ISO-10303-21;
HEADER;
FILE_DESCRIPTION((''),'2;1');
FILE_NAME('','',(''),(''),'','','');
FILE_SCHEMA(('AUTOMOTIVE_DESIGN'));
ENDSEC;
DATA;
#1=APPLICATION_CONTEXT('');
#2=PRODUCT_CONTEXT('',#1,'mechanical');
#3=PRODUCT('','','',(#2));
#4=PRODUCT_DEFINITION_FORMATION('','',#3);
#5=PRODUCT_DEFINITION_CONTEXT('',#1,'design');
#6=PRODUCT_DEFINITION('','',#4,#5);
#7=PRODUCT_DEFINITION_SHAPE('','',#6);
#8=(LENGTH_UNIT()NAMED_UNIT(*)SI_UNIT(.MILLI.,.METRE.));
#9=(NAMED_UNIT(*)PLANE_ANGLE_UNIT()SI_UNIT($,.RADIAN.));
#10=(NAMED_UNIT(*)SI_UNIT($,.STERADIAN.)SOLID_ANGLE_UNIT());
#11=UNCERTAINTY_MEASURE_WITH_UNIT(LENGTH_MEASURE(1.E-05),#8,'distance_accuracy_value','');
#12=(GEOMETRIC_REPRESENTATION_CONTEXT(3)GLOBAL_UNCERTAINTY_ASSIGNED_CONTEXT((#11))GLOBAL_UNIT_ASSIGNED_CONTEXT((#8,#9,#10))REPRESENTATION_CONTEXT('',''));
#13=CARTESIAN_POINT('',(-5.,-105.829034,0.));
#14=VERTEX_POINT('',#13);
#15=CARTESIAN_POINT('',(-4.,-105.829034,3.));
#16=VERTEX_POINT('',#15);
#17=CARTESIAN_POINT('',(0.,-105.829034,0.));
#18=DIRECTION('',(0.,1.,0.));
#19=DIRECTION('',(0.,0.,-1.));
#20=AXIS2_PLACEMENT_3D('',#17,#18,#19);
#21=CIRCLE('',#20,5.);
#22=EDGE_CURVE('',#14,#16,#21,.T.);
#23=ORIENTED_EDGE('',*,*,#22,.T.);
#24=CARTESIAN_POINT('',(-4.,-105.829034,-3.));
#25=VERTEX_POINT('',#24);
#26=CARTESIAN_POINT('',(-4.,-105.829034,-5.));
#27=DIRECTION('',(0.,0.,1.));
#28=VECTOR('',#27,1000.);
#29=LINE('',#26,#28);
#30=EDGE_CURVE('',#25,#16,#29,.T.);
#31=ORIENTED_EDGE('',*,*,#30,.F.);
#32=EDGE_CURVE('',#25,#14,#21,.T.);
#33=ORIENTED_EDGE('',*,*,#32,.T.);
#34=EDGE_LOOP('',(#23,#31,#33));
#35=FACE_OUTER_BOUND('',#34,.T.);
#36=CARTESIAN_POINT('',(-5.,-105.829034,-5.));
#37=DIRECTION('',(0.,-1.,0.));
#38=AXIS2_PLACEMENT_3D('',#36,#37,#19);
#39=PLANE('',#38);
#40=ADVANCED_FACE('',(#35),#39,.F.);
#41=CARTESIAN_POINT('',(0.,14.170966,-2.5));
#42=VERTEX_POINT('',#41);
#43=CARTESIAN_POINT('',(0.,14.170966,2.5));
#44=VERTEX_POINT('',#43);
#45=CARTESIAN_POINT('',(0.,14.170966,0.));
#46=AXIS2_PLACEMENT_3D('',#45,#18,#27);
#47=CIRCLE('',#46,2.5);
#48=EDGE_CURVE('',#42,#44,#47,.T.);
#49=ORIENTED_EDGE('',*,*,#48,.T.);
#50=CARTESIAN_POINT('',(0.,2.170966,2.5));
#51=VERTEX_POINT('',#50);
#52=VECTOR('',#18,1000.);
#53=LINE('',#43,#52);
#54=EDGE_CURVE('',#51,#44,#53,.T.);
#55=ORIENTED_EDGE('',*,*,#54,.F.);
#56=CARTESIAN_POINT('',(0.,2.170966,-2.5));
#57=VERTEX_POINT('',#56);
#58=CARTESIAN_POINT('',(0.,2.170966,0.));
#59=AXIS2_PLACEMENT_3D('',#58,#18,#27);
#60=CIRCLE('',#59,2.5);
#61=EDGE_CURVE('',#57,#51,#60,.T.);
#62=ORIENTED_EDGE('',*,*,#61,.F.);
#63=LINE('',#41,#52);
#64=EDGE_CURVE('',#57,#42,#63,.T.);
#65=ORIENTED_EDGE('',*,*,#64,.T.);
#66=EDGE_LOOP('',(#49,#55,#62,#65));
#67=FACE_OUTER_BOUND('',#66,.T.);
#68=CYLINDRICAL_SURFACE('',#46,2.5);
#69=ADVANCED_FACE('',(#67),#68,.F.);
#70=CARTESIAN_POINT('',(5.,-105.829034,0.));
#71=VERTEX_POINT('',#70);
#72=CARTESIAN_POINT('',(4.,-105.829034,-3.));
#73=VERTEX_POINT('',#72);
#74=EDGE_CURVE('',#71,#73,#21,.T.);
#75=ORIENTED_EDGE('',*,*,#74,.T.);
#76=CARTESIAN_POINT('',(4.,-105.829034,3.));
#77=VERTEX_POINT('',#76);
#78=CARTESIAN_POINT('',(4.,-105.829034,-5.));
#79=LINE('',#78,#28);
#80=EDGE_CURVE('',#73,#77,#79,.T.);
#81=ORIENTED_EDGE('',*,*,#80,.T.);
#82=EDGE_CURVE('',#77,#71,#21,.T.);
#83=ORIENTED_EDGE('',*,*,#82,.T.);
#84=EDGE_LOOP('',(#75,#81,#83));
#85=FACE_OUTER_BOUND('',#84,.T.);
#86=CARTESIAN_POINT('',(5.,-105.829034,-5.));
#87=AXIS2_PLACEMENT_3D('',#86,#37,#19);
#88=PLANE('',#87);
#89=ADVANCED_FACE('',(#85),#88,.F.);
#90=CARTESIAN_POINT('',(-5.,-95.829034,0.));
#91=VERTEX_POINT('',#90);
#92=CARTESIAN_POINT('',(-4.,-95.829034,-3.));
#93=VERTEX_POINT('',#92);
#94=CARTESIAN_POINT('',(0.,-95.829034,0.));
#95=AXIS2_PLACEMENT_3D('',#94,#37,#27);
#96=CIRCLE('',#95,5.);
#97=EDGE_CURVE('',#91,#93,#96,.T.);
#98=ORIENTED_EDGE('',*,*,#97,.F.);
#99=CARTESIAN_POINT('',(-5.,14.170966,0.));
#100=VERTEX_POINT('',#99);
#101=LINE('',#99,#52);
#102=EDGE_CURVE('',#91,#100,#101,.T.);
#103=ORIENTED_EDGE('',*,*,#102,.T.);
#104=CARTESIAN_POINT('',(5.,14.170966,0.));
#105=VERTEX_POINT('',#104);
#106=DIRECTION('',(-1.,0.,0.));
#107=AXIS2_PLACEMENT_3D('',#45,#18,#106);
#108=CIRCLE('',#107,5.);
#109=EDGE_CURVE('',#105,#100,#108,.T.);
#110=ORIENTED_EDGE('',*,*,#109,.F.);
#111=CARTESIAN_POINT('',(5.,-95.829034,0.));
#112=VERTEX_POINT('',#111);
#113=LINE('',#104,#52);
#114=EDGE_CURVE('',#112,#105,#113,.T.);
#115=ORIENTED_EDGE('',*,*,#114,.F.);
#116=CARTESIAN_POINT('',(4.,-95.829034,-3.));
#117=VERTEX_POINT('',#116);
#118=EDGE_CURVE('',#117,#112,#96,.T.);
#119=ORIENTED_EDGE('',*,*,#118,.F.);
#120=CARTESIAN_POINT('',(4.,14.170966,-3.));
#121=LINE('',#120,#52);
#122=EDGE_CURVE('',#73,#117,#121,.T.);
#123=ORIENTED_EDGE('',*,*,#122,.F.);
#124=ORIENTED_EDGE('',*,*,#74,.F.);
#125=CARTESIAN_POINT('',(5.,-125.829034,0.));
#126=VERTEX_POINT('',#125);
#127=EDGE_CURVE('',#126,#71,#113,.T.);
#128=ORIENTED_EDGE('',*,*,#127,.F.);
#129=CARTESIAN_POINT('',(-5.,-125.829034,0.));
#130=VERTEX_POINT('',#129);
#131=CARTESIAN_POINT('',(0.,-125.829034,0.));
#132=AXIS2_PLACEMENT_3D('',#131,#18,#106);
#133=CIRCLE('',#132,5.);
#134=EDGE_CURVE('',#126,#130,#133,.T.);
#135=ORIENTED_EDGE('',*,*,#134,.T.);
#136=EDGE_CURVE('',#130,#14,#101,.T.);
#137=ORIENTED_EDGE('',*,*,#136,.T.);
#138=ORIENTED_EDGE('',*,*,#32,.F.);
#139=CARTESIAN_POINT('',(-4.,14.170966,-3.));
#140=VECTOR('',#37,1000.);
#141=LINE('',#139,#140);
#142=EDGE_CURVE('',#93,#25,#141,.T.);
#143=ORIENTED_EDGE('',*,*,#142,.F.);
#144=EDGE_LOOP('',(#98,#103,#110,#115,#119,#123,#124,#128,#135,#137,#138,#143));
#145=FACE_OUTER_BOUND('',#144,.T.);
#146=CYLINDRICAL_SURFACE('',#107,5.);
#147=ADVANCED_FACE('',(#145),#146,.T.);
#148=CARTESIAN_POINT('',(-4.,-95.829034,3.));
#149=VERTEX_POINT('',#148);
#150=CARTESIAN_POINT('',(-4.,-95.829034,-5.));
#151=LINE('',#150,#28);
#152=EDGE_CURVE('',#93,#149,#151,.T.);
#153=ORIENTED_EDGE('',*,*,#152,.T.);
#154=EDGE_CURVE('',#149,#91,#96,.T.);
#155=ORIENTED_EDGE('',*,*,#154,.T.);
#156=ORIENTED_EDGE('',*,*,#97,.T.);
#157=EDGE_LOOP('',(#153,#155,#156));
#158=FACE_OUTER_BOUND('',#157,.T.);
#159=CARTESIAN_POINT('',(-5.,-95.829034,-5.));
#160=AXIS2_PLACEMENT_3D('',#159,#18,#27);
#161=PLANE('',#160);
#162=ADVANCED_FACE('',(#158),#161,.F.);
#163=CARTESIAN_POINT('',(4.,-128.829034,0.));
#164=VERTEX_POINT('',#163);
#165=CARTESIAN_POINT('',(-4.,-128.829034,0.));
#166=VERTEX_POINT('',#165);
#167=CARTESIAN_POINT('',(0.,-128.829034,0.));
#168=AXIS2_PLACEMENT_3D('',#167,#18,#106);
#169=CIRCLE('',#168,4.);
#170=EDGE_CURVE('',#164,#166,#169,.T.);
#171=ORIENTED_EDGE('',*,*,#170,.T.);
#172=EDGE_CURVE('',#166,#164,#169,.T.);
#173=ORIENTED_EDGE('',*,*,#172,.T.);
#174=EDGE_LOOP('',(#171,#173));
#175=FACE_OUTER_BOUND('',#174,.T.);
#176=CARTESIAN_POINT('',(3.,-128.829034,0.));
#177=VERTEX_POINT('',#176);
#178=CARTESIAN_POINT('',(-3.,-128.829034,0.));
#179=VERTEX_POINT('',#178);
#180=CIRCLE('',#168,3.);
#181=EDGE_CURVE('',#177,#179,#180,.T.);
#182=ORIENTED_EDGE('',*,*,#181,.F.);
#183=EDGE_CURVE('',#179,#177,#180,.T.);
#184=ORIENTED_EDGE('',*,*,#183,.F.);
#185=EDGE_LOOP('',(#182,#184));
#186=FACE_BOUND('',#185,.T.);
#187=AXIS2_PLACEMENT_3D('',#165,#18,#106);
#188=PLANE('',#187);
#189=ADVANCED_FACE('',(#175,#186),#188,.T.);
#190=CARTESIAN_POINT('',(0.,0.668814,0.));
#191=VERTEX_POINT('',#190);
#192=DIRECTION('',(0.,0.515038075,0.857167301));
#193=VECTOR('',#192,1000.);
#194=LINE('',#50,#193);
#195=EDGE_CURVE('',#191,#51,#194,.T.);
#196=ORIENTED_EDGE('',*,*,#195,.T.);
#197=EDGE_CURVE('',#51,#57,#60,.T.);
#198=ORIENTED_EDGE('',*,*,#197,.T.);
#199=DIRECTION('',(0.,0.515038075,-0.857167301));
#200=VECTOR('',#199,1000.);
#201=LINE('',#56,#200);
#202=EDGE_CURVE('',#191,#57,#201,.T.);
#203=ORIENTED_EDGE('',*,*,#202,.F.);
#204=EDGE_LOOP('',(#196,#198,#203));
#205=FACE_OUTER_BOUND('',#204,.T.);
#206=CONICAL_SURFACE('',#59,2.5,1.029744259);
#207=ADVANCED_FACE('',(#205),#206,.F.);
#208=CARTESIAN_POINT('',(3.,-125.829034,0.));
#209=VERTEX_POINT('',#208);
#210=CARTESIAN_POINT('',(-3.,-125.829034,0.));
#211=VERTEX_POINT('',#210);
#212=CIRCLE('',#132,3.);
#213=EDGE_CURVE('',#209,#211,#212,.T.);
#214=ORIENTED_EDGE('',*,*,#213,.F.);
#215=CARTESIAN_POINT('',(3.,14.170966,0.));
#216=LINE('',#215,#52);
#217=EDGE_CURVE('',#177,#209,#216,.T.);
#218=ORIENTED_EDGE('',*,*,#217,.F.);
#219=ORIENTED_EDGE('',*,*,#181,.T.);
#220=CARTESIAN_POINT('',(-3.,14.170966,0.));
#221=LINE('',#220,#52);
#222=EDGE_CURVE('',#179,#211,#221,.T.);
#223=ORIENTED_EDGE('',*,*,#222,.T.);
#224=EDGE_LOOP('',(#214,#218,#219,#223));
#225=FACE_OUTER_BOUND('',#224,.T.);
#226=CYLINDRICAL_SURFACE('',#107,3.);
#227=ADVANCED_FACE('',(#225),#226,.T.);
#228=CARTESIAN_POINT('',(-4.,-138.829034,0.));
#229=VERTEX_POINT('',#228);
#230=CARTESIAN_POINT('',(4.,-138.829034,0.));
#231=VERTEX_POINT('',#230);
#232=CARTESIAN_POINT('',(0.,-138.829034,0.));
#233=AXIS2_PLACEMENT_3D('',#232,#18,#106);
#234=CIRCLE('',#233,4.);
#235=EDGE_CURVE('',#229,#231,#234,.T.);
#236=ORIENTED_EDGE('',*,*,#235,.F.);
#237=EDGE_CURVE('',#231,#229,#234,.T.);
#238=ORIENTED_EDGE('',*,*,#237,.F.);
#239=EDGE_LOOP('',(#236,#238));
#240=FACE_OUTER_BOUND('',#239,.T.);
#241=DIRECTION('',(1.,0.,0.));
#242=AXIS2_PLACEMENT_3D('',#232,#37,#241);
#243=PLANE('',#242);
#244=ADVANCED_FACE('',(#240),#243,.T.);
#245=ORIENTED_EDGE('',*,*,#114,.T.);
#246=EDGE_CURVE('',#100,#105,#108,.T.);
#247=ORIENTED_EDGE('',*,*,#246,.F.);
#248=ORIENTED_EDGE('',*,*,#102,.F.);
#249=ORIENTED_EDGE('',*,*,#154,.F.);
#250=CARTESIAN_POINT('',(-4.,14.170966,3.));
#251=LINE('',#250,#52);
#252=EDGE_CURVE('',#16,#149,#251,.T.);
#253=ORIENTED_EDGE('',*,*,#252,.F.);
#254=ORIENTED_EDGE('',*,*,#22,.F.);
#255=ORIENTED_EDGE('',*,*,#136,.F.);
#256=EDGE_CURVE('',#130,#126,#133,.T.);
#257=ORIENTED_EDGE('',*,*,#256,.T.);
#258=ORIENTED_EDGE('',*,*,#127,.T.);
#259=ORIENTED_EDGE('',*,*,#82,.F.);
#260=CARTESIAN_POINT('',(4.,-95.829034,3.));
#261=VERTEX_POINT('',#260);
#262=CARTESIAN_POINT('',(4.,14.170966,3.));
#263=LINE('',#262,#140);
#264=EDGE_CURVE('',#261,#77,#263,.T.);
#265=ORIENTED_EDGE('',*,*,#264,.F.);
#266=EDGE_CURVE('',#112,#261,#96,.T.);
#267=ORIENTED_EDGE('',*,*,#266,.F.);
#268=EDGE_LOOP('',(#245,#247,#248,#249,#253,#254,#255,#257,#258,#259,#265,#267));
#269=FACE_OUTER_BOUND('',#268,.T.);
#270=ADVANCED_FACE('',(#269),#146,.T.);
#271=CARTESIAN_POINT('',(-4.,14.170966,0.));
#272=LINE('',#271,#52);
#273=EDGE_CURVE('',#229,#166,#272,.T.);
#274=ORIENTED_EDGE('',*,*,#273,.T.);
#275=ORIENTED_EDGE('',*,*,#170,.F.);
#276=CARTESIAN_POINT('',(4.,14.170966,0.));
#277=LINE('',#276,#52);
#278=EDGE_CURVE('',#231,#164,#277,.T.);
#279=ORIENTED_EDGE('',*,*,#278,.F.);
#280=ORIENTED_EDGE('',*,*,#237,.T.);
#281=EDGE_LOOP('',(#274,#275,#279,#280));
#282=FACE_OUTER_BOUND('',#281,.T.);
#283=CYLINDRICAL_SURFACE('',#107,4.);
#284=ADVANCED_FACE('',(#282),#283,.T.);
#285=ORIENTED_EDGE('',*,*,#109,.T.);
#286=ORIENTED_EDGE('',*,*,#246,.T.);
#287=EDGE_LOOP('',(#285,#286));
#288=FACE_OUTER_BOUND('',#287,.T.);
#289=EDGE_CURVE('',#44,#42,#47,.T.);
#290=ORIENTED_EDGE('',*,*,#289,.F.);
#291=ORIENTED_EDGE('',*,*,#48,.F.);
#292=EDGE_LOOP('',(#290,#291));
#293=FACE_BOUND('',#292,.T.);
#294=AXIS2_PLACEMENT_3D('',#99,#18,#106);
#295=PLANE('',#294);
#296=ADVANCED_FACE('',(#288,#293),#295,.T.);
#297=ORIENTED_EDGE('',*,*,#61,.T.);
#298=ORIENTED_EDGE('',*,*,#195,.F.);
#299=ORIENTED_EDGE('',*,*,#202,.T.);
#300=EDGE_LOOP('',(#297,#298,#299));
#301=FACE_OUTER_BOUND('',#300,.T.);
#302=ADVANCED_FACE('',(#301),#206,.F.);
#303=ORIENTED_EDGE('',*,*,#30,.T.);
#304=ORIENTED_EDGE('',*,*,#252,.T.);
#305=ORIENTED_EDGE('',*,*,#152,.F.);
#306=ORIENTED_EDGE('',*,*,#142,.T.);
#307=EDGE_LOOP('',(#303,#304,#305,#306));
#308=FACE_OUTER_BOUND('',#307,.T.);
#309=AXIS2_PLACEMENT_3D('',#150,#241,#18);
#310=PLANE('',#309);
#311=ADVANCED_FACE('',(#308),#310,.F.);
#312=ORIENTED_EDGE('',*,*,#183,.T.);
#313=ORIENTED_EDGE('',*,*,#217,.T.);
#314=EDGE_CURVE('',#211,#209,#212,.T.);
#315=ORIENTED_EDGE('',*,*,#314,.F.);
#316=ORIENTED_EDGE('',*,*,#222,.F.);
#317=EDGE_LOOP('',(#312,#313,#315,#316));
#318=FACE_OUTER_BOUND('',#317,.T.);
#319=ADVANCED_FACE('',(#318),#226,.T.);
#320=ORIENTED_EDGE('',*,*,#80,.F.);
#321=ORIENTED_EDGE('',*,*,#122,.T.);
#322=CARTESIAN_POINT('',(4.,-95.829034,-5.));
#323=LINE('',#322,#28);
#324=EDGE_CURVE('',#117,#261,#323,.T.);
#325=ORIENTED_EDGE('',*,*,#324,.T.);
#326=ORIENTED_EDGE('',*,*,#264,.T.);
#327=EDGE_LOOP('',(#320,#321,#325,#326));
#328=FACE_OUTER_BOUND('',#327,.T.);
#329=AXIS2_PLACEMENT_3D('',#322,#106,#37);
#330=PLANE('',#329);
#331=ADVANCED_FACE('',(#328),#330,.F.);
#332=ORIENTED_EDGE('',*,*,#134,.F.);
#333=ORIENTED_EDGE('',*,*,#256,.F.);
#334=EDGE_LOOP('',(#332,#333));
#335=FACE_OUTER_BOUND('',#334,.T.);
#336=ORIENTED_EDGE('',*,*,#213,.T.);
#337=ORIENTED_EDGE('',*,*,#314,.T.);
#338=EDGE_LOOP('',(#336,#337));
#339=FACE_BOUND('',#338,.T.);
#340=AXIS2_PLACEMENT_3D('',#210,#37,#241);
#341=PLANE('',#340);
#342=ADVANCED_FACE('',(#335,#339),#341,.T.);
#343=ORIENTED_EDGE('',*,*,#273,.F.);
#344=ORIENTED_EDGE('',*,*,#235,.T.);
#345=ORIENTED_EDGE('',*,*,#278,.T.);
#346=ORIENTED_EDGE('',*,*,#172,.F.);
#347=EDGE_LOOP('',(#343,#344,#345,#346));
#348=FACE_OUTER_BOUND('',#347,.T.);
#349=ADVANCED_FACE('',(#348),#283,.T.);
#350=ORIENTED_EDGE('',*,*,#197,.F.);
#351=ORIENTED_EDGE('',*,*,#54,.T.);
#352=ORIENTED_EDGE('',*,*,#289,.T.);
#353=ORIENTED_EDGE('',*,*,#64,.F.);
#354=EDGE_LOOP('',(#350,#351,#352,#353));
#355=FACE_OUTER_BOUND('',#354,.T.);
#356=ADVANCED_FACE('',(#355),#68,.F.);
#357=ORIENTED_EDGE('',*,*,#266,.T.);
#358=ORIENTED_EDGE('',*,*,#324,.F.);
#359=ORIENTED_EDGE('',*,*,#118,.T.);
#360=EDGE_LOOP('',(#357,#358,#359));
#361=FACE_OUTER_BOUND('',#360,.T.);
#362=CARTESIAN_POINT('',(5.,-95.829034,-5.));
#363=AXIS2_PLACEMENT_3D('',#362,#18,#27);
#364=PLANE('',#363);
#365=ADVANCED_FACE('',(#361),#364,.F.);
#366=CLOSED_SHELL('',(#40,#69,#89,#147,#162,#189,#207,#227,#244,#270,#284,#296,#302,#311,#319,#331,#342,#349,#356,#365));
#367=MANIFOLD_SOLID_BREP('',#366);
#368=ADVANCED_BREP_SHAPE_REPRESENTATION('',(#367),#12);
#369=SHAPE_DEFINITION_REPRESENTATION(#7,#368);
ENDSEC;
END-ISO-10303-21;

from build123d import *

# Parameters (mm, degrees)
CUT_EXTRUDE1_DEPTH      = 140.008995048
CUT_EXTRUDE1_DEPTH_BACK = 140.008995048
SKETCH2_W               = 1
SKETCH2_H               = 10
M6_TAPPED_HOLE1_D       = 5
M6_TAPPED_HOLE1_DEPTH   = 12
M6_TAPPED_HOLE1_TIP     = 1.502151548


with BuildPart() as part:
    # Sketch1 → Revolve1 (revolve)
    with BuildSketch(Plane.XY):
        Polygon((0, 14.170965918), (0, -138.829034082), (-4, -138.829034082), (-4, -128.829034082), (-3, -128.829034082), (-3, -125.829034082), (-5, -125.829034082), (-5, 14.170965918), align=None)
    revolve(axis=Axis((0, 14.170965918, 0), (0, -1, 0)))

    # Sketch2 → Cut-Extrude1 (cut, two sides: drawn at the far end of the back side and taken through both)
    with BuildSketch(Plane.XY.offset(-CUT_EXTRUDE1_DEPTH_BACK)):
        with Locations((-4.5, -100.829034082)):
            Rectangle(SKETCH2_W, SKETCH2_H)
        with Locations((4.5, -100.829034082)):
            Rectangle(SKETCH2_W, SKETCH2_H)
    extrude(amount=CUT_EXTRUDE1_DEPTH + CUT_EXTRUDE1_DEPTH_BACK, mode=Mode.SUBTRACT)

    # M6 Tapped Hole1
    with Locations(Plane(origin=(0, 14.170965918, 0), x_dir=(1, 0, 0), z_dir=(0, 1, 0))):
        with Locations((0, 0)):
            Hole(M6_TAPPED_HOLE1_D / 2, depth=M6_TAPPED_HOLE1_DEPTH)
            with Locations((0, 0, -(M6_TAPPED_HOLE1_DEPTH + M6_TAPPED_HOLE1_TIP / 2))):  # 118° drill point
                Cone(0, M6_TAPPED_HOLE1_D / 2, M6_TAPPED_HOLE1_TIP, mode=Mode.SUBTRACT)


solid = part.part
